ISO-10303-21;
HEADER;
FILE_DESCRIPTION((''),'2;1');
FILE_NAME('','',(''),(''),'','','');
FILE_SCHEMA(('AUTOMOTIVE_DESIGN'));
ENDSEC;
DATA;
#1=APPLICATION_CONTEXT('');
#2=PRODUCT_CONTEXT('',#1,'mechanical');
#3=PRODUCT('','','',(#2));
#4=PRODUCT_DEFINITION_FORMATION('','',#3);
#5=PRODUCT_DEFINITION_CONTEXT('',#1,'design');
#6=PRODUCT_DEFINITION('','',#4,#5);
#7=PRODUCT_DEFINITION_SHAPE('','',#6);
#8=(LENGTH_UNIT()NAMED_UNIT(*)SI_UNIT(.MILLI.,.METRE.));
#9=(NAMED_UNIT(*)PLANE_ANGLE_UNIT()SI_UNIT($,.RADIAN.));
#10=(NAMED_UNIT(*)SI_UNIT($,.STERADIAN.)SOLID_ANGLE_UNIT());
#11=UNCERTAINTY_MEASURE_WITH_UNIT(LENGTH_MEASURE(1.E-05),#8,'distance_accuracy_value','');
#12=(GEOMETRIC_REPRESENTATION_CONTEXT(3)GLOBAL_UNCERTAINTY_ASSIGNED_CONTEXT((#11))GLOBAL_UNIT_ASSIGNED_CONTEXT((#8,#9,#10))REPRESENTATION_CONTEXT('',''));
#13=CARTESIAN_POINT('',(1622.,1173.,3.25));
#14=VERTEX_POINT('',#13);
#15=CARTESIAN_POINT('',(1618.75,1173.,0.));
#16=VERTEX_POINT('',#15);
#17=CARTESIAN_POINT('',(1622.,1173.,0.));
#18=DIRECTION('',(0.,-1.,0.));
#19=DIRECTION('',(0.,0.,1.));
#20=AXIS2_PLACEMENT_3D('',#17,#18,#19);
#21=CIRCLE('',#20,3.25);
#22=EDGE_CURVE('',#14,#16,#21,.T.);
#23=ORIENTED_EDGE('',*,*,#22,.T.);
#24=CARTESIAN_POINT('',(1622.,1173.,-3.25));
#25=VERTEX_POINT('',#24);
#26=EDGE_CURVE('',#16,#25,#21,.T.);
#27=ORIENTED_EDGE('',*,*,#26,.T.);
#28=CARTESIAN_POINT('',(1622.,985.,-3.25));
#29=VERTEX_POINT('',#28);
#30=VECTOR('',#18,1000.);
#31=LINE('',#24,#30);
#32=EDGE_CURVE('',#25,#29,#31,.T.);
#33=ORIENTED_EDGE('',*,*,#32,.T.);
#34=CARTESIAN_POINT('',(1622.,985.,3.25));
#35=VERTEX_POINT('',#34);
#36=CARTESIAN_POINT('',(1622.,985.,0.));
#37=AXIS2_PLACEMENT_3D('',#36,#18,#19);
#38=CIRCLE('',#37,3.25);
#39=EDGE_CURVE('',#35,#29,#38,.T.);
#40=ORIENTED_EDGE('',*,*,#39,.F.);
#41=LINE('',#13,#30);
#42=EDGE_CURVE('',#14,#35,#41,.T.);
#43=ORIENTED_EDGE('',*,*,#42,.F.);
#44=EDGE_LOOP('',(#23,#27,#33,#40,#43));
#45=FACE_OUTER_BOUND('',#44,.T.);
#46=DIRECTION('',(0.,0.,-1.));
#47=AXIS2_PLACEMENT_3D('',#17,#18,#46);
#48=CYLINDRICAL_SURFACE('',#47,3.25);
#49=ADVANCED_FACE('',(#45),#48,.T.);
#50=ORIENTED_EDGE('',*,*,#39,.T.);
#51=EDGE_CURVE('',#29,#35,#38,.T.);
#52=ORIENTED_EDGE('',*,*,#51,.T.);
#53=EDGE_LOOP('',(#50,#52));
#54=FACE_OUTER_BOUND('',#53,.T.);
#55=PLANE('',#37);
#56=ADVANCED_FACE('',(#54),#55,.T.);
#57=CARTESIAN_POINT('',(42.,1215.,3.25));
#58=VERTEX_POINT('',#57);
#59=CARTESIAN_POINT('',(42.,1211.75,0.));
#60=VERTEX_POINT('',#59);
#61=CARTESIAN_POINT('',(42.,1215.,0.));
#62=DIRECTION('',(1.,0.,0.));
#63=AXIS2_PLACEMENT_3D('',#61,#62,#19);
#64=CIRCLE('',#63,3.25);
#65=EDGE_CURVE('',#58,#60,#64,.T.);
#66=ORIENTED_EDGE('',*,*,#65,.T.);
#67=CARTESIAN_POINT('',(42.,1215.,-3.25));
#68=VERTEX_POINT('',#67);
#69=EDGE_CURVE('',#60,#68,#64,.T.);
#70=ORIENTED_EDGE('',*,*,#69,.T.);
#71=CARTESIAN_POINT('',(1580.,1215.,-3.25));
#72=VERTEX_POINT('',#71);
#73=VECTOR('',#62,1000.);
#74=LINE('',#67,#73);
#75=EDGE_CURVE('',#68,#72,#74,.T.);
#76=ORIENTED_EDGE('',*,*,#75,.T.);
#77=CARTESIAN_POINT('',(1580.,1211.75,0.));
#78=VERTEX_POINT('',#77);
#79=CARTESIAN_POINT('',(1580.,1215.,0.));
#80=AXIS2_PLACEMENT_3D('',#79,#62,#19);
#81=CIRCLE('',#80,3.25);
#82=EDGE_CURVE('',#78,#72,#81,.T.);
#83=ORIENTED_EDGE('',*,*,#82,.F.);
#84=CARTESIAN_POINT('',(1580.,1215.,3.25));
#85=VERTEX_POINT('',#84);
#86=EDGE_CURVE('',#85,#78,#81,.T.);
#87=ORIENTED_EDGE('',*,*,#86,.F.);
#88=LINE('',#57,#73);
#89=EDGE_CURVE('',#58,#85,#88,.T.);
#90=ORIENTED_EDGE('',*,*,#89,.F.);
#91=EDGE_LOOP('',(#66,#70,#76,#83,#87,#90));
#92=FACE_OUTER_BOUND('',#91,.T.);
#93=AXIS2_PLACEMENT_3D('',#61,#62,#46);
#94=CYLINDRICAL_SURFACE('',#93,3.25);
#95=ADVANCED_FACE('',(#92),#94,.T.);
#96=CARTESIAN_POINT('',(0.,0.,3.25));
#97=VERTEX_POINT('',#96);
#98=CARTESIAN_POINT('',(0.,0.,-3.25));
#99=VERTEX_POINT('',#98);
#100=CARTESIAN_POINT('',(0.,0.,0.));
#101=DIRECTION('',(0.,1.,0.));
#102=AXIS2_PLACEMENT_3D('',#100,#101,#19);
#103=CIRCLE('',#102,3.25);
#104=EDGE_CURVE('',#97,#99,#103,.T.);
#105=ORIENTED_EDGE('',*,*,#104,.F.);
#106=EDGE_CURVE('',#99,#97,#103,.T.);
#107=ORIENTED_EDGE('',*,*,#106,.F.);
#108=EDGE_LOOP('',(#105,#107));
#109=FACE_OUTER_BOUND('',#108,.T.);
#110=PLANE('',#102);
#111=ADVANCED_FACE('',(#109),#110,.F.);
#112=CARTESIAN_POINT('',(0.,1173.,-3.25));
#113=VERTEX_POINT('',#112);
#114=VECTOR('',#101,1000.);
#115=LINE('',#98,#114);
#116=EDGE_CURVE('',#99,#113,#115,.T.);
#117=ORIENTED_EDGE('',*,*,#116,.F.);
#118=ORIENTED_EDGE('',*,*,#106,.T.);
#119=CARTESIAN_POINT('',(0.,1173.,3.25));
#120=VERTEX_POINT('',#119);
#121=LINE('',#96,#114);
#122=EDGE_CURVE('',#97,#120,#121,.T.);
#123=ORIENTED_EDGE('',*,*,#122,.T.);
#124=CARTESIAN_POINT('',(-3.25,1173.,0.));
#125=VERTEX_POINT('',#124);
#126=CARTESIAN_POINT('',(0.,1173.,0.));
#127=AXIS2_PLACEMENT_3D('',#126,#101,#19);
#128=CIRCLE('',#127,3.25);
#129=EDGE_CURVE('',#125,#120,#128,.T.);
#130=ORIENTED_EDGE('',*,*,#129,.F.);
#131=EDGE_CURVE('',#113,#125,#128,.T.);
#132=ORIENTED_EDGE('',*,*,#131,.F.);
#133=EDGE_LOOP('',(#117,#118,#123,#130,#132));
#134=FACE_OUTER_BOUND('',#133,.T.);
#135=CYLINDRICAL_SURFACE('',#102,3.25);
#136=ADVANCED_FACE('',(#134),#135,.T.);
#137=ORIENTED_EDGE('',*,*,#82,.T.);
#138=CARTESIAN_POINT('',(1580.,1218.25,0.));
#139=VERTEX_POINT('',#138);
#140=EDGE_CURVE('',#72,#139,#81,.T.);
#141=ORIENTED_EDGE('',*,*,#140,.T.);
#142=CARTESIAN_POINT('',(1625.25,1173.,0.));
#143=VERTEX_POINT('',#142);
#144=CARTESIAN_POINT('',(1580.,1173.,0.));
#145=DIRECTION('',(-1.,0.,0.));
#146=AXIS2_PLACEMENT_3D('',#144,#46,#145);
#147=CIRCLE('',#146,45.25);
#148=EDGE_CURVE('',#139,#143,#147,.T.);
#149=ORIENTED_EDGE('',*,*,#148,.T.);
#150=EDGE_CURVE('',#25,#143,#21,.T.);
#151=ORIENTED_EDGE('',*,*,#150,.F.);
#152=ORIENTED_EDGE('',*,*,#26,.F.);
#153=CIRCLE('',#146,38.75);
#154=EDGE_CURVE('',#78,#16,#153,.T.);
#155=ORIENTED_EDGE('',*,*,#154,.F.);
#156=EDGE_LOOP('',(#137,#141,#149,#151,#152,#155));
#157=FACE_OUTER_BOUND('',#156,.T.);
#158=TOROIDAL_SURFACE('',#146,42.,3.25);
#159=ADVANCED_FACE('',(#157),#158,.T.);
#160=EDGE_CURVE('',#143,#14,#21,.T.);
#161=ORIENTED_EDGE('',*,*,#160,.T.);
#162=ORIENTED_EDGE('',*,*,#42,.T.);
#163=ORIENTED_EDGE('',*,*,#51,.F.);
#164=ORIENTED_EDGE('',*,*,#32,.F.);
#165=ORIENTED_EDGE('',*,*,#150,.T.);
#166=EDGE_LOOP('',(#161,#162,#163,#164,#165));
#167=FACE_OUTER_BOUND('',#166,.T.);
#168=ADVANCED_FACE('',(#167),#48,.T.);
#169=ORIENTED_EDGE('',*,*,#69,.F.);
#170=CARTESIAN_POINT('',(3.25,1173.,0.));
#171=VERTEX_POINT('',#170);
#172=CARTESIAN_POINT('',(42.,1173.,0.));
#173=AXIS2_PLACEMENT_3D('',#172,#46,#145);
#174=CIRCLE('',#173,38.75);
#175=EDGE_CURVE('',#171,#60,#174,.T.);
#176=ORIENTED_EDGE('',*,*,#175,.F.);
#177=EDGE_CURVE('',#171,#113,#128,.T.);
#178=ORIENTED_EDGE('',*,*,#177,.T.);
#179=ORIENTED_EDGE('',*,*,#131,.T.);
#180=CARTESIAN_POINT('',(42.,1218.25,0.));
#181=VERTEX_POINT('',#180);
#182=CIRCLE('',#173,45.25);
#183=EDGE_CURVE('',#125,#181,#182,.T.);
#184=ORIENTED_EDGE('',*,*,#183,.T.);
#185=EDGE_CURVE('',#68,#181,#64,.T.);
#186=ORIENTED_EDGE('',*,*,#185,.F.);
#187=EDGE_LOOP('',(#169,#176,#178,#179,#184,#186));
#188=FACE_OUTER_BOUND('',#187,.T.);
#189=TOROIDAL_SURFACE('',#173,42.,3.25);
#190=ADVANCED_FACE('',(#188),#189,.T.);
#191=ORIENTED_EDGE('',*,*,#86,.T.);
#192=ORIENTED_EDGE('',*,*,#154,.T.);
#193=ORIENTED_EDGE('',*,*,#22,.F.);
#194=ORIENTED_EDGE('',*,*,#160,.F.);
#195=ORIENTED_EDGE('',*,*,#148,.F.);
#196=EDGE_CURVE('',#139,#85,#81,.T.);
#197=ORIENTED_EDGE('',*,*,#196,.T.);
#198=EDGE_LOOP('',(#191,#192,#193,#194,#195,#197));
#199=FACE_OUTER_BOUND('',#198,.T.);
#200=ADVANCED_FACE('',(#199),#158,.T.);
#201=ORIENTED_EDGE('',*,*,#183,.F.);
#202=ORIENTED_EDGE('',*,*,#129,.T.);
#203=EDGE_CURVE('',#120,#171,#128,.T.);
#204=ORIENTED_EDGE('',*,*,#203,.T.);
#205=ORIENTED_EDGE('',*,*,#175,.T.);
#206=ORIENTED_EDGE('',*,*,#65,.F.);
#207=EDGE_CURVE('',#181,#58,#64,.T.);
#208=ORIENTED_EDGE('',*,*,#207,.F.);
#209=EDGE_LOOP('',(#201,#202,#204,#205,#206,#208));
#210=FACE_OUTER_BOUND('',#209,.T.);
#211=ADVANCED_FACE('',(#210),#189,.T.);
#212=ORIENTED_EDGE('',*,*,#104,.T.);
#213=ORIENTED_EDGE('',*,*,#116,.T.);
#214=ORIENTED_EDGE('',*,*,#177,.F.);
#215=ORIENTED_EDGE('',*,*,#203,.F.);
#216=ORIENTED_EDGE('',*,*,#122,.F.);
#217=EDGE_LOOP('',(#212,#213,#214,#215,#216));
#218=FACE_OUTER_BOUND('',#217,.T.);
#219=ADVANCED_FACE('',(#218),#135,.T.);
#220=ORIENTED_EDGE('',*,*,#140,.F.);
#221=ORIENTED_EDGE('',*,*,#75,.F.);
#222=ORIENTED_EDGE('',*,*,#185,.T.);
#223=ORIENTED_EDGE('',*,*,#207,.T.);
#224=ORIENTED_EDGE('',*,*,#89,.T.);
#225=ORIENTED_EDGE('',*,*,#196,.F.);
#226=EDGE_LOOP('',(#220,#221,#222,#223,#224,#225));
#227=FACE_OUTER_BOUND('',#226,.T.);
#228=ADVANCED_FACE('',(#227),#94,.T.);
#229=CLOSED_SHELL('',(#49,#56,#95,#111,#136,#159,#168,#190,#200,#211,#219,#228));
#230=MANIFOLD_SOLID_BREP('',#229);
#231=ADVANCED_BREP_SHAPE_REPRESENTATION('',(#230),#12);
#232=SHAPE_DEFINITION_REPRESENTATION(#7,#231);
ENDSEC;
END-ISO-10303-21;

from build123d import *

# Parameters (mm, degrees)
SKETCH2_R = 3.25


with BuildPart() as part:
    # Sweep1: sweep along a path in Sketch1
    with BuildLine(Plane.XY) as sweep1_path:
        Line((0, 0), (0, 1173))
        ThreePointArc((0, 1173), (12.30151519, 1202.69848481), (42, 1215))
        Line((42, 1215), (1580, 1215))
        ThreePointArc((1580, 1215), (1609.69848481, 1202.69848481), (1622, 1173))
        Line((1622, 1173), (1622, 985))
    # Sketch2 → Sweep1 (sweep)
    with BuildSketch(Plane(origin=(0, 0, 0), x_dir=(1, 0, 0), z_dir=(0, 1, 0))):
        Circle(SKETCH2_R)
    sweep(path=sweep1_path.line)


solid = part.part
